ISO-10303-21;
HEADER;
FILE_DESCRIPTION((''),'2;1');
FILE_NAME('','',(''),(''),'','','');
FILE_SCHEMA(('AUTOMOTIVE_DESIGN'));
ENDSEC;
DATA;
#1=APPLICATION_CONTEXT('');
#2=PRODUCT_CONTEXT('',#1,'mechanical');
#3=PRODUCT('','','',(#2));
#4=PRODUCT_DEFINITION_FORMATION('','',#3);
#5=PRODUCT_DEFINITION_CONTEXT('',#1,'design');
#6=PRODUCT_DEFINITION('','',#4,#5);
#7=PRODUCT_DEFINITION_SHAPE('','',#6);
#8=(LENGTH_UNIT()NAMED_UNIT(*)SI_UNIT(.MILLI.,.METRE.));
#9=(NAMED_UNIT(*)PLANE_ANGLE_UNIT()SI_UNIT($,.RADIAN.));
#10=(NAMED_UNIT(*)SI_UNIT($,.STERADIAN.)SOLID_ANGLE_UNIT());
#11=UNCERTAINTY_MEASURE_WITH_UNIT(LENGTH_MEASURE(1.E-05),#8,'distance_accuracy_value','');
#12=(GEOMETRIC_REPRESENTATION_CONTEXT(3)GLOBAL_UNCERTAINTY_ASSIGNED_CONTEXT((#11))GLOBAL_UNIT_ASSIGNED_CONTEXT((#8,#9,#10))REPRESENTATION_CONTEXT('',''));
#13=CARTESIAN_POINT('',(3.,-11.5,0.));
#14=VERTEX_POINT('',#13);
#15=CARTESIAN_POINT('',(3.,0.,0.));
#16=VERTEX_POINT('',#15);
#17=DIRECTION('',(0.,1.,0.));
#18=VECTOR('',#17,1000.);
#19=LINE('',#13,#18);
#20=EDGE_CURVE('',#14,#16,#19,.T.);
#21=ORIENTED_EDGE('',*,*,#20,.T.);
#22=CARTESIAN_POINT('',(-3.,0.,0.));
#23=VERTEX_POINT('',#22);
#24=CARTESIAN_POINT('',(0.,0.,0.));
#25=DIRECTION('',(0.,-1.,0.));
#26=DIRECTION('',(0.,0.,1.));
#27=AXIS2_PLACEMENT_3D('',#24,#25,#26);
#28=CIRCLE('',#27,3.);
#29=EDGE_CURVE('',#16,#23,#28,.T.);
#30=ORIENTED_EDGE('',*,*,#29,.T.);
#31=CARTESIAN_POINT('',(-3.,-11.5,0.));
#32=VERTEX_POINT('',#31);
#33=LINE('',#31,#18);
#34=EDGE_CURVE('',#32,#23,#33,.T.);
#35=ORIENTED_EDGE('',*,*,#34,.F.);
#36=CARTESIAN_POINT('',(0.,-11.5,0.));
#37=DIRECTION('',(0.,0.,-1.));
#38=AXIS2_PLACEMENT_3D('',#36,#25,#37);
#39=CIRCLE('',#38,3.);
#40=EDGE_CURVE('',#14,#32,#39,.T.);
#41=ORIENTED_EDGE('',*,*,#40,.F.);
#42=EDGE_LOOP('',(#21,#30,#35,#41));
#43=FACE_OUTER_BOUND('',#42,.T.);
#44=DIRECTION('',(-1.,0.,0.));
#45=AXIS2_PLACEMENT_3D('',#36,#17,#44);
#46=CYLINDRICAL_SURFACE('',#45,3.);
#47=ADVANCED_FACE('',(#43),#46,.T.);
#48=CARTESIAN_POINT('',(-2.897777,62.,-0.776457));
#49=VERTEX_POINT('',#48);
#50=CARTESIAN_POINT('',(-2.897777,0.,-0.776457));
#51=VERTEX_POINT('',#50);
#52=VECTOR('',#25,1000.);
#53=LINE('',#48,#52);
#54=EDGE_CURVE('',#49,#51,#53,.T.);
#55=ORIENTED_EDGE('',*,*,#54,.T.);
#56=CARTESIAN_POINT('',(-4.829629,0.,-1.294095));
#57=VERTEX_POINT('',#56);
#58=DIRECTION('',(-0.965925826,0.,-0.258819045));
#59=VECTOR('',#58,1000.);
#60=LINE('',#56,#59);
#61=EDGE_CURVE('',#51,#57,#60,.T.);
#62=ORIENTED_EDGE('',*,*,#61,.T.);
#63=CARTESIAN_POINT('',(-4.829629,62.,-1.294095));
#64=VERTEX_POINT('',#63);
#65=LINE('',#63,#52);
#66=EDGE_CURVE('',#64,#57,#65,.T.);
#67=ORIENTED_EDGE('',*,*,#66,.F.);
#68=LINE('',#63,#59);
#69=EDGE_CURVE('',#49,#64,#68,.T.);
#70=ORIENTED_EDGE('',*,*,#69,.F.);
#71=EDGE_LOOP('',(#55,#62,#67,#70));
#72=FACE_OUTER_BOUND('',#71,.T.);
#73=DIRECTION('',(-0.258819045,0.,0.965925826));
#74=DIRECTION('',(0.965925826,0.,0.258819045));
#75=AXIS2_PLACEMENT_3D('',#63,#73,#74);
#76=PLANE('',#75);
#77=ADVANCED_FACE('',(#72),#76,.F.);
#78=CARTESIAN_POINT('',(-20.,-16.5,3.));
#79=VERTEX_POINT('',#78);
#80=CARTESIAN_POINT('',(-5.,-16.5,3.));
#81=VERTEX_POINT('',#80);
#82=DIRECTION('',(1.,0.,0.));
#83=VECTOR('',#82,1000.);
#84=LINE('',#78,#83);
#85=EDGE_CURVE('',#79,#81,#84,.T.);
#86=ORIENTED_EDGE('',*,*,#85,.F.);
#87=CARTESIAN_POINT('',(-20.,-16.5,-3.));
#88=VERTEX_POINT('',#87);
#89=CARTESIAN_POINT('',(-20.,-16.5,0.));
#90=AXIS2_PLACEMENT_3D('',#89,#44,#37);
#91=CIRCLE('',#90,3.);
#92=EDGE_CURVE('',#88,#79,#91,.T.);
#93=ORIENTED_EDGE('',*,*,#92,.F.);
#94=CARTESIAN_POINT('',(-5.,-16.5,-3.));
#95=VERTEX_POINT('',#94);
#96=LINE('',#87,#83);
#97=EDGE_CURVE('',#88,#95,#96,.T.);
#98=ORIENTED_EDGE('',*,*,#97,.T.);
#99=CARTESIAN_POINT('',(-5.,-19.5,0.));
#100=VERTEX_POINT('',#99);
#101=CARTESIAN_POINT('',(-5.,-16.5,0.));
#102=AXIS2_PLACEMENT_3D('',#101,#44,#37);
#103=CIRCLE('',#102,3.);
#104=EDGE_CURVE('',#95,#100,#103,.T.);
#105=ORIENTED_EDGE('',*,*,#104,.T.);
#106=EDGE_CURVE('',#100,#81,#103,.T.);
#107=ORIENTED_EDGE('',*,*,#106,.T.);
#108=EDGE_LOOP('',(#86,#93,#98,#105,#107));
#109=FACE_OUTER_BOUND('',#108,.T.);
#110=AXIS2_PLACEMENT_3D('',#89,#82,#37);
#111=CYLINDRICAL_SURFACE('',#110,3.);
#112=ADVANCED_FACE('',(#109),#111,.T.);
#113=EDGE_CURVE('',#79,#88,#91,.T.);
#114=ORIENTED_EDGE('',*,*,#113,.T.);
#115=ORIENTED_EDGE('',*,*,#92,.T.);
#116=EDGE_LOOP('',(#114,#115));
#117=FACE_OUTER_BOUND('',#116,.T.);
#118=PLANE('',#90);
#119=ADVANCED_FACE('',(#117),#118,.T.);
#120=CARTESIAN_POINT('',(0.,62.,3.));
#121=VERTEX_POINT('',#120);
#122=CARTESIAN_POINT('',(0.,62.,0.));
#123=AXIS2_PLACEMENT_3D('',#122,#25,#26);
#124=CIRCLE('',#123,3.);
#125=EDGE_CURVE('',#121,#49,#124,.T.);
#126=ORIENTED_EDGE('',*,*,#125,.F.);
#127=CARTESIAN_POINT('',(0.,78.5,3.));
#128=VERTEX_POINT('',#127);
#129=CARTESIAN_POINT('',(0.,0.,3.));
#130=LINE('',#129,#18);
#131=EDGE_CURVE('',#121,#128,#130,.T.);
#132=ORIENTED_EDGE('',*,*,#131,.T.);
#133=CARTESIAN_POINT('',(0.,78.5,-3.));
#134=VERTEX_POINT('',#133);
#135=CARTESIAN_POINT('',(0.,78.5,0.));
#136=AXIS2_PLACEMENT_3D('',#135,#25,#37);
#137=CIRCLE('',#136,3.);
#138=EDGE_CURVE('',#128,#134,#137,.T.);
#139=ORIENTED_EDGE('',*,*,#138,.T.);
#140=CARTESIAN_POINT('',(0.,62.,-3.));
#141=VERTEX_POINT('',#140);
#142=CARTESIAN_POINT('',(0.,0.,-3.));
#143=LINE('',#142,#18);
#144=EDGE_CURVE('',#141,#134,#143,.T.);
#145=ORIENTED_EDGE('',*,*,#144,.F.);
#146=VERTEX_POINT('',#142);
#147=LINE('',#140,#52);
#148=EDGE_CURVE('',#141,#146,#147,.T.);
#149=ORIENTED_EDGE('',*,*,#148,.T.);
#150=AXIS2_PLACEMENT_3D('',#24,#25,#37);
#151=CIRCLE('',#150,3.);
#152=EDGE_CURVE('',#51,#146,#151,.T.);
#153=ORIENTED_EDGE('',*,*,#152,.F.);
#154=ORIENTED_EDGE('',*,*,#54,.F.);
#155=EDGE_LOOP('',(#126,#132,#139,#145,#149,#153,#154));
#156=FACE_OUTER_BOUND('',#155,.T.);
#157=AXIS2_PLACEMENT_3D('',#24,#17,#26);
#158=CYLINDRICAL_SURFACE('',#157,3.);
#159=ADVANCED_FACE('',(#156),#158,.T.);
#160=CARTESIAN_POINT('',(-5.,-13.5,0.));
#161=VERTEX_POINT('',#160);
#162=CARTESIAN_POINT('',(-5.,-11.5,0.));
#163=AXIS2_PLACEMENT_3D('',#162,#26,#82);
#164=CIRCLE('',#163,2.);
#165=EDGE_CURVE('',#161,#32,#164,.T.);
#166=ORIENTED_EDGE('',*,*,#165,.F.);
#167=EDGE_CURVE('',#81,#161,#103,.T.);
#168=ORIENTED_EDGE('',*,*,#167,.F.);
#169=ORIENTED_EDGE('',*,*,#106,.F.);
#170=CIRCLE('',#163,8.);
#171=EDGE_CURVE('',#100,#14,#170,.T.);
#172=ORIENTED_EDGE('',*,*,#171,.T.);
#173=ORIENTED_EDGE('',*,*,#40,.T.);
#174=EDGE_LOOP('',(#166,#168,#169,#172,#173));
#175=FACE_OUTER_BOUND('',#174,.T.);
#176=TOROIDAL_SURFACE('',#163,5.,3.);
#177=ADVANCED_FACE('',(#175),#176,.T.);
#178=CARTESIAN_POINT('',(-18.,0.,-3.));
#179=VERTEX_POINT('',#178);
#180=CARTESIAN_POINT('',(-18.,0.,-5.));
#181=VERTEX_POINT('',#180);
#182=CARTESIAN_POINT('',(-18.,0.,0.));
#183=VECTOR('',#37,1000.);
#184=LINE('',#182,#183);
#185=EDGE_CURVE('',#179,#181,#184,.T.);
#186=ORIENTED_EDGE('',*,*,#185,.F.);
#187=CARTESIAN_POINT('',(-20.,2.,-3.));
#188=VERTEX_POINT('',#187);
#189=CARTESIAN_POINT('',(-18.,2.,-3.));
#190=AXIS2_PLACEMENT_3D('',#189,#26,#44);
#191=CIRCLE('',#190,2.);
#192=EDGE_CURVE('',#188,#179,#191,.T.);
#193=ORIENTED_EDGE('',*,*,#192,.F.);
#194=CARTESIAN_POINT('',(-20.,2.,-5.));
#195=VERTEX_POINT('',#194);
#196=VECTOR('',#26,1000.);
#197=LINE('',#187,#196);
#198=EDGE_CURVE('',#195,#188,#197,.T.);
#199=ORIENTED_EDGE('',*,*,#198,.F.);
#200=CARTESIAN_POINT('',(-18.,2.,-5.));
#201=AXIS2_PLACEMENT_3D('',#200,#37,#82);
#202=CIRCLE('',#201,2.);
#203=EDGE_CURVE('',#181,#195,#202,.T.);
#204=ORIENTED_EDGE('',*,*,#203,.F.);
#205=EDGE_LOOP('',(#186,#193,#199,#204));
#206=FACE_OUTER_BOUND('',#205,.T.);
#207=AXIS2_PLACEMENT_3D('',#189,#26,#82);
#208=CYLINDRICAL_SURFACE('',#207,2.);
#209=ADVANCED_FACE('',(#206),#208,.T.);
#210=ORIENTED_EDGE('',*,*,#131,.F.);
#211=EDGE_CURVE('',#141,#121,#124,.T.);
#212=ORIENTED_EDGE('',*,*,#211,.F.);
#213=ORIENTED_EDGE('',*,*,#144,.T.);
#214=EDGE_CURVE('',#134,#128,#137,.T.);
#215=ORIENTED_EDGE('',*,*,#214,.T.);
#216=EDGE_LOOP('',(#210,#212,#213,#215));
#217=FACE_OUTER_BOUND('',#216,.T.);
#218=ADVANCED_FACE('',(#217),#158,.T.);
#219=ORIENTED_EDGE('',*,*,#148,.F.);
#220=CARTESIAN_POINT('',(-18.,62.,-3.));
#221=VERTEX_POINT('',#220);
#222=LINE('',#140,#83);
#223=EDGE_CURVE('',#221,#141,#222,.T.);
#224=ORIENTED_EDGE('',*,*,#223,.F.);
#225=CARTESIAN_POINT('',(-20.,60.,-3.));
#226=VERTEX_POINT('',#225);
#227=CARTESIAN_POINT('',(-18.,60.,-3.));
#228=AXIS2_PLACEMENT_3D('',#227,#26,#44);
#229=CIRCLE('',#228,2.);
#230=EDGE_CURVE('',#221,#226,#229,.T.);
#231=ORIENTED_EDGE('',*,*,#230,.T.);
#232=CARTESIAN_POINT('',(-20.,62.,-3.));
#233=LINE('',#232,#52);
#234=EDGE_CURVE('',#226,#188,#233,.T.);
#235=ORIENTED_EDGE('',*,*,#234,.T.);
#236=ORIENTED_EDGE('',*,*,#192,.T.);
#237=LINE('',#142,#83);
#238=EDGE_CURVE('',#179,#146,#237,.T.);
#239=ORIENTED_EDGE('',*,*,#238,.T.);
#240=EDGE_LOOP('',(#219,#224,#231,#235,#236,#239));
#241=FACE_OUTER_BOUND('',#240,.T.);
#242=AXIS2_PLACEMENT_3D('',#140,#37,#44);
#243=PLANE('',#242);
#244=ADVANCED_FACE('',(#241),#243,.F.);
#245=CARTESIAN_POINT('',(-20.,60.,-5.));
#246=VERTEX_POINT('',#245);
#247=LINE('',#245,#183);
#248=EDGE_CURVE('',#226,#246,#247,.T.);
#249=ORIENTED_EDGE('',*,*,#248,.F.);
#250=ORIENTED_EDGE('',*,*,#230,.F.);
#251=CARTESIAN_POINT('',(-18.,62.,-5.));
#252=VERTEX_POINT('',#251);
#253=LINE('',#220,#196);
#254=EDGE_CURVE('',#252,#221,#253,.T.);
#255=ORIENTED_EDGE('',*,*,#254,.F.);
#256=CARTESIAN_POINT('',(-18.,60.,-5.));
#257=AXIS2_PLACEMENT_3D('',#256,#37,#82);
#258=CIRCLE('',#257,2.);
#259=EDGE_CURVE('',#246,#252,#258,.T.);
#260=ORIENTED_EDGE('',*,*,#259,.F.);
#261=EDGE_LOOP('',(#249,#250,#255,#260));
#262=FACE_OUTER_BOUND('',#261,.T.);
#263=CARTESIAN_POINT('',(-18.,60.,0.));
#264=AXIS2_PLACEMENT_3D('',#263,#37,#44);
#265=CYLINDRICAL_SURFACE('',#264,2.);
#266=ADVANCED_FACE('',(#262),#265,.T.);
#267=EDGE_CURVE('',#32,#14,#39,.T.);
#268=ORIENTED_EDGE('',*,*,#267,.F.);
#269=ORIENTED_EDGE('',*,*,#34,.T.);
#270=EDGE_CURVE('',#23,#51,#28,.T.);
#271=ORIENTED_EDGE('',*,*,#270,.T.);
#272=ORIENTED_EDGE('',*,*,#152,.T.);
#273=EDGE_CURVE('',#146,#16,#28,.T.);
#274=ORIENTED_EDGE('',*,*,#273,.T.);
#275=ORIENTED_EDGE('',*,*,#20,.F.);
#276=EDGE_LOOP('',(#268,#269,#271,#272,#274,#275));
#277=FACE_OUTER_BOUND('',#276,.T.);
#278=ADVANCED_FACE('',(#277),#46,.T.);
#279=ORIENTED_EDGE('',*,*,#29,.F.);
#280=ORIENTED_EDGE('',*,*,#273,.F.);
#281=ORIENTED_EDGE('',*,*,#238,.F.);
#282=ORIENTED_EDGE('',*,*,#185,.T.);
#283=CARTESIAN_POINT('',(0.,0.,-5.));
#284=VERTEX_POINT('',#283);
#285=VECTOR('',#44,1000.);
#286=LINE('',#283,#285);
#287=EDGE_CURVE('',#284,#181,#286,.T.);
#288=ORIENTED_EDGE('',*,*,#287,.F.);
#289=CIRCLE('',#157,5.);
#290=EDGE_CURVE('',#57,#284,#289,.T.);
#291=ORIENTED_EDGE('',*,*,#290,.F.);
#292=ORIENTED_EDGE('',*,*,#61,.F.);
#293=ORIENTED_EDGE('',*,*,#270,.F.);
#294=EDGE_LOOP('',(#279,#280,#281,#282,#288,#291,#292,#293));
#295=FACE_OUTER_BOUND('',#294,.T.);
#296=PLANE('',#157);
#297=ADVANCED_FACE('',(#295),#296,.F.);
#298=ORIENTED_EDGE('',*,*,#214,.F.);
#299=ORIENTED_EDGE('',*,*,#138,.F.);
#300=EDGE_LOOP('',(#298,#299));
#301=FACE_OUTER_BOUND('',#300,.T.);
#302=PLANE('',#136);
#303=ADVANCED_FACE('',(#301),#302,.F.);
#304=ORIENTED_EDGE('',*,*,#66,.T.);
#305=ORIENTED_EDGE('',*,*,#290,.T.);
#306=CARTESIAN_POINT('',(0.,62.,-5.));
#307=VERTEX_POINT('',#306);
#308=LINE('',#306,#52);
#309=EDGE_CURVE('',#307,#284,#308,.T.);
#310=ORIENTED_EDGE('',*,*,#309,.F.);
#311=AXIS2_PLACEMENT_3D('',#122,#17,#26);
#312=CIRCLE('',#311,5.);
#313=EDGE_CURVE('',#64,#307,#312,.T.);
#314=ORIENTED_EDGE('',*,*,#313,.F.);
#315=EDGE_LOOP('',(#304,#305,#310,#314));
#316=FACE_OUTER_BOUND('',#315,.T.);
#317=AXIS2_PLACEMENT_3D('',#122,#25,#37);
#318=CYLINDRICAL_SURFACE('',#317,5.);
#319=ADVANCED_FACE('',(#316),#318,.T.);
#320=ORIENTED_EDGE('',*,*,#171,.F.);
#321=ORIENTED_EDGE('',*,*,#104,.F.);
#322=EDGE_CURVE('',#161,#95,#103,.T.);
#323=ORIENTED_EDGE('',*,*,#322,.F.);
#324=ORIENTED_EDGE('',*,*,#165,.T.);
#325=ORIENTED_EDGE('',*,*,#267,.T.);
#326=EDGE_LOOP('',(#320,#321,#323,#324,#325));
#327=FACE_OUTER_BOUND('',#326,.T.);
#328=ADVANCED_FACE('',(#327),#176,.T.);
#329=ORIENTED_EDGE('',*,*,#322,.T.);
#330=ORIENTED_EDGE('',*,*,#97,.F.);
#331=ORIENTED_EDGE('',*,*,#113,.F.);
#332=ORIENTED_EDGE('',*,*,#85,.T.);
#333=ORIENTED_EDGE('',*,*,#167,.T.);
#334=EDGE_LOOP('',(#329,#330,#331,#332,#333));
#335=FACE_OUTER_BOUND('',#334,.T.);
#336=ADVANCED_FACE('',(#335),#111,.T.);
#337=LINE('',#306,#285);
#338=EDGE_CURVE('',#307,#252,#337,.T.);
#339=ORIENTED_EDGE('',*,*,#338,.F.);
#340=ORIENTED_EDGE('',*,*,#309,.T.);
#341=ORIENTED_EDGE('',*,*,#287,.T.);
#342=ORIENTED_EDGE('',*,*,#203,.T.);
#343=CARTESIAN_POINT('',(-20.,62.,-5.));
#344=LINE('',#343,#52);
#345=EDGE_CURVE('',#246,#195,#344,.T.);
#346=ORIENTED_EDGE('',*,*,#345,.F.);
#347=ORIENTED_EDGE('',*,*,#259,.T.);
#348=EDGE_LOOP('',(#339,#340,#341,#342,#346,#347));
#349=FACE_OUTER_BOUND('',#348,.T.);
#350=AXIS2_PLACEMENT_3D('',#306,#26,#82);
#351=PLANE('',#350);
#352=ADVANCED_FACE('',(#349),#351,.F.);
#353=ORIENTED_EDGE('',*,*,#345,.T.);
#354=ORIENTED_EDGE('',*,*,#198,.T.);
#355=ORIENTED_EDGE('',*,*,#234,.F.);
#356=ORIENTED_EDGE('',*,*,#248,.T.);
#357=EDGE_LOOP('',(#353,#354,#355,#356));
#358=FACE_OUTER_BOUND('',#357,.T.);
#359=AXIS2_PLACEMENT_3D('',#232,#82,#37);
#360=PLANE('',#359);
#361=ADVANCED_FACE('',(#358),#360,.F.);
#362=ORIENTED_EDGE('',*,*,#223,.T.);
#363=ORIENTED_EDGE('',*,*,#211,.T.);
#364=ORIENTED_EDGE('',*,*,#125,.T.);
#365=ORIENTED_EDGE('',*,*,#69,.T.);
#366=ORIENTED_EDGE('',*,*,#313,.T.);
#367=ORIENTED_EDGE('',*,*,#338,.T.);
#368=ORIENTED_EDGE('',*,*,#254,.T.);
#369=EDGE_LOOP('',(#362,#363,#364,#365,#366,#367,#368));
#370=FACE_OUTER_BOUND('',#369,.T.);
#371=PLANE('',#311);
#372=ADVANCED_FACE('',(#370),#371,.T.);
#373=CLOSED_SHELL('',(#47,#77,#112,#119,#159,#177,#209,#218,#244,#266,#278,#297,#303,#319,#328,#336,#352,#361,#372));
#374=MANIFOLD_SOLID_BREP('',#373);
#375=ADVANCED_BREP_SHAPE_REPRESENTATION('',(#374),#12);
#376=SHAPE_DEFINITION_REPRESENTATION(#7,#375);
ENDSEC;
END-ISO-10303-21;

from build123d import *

# Parameters (mm, degrees)
BOSS_EXTRUDE1_DEPTH = 62
SWEEP1_PROFILE_R    = 3
FILLET3_R           = 2


with BuildPart() as part:
    # Sketch1 → Boss-Extrude1 (new body)
    with BuildSketch(Plane(origin=(0, 0, 0), x_dir=(1, 0, 0), z_dir=(0, 1, 0))):
        with BuildLine():
            Line((0, 5), (-20, 5))
            Line((-20, 5), (-20, 3))
            Line((-20, 3), (0, 3))
            ThreePointArc((0, 3), (1.826284287, -2.380060021), (-2.897777479, 0.776457135))
            Line((-2.897777479, 0.776457135), (-4.829629131, 1.294095226))
            ThreePointArc((-4.829629131, 1.294095226), (3.043807145, -3.966766701), (0, 5))
        make_face()
    extrude(amount=BOSS_EXTRUDE1_DEPTH)

    # Sweep1: sweep along a path in Sketch2
    with BuildLine(Plane.XY) as sweep1_path:
        Line((0, 78.5), (0, 0))
        Line((0, 0), (0, -11.5))
        ThreePointArc((0, -11.5), (-1.464466094, -15.035533906), (-5, -16.5))
        Line((-5, -16.5), (-20, -16.5))
    # Sweep1 profile (on start of the path) → Sweep1 (sweep)
    with BuildSketch(Plane(origin=(0, 78.5, 0), x_dir=(0, 0, -1), z_dir=(0, -1, 0))):
        Circle(SWEEP1_PROFILE_R)
    sweep(path=sweep1_path.line)

    # Fillet3
    fillet3_edges = [part.edges().sort_by_distance(p)[0] for p in [
        (-20, 62, -4),
        (-20, 0, -4),
    ]]
    fillet(fillet3_edges, radius=FILLET3_R)


solid = part.part
